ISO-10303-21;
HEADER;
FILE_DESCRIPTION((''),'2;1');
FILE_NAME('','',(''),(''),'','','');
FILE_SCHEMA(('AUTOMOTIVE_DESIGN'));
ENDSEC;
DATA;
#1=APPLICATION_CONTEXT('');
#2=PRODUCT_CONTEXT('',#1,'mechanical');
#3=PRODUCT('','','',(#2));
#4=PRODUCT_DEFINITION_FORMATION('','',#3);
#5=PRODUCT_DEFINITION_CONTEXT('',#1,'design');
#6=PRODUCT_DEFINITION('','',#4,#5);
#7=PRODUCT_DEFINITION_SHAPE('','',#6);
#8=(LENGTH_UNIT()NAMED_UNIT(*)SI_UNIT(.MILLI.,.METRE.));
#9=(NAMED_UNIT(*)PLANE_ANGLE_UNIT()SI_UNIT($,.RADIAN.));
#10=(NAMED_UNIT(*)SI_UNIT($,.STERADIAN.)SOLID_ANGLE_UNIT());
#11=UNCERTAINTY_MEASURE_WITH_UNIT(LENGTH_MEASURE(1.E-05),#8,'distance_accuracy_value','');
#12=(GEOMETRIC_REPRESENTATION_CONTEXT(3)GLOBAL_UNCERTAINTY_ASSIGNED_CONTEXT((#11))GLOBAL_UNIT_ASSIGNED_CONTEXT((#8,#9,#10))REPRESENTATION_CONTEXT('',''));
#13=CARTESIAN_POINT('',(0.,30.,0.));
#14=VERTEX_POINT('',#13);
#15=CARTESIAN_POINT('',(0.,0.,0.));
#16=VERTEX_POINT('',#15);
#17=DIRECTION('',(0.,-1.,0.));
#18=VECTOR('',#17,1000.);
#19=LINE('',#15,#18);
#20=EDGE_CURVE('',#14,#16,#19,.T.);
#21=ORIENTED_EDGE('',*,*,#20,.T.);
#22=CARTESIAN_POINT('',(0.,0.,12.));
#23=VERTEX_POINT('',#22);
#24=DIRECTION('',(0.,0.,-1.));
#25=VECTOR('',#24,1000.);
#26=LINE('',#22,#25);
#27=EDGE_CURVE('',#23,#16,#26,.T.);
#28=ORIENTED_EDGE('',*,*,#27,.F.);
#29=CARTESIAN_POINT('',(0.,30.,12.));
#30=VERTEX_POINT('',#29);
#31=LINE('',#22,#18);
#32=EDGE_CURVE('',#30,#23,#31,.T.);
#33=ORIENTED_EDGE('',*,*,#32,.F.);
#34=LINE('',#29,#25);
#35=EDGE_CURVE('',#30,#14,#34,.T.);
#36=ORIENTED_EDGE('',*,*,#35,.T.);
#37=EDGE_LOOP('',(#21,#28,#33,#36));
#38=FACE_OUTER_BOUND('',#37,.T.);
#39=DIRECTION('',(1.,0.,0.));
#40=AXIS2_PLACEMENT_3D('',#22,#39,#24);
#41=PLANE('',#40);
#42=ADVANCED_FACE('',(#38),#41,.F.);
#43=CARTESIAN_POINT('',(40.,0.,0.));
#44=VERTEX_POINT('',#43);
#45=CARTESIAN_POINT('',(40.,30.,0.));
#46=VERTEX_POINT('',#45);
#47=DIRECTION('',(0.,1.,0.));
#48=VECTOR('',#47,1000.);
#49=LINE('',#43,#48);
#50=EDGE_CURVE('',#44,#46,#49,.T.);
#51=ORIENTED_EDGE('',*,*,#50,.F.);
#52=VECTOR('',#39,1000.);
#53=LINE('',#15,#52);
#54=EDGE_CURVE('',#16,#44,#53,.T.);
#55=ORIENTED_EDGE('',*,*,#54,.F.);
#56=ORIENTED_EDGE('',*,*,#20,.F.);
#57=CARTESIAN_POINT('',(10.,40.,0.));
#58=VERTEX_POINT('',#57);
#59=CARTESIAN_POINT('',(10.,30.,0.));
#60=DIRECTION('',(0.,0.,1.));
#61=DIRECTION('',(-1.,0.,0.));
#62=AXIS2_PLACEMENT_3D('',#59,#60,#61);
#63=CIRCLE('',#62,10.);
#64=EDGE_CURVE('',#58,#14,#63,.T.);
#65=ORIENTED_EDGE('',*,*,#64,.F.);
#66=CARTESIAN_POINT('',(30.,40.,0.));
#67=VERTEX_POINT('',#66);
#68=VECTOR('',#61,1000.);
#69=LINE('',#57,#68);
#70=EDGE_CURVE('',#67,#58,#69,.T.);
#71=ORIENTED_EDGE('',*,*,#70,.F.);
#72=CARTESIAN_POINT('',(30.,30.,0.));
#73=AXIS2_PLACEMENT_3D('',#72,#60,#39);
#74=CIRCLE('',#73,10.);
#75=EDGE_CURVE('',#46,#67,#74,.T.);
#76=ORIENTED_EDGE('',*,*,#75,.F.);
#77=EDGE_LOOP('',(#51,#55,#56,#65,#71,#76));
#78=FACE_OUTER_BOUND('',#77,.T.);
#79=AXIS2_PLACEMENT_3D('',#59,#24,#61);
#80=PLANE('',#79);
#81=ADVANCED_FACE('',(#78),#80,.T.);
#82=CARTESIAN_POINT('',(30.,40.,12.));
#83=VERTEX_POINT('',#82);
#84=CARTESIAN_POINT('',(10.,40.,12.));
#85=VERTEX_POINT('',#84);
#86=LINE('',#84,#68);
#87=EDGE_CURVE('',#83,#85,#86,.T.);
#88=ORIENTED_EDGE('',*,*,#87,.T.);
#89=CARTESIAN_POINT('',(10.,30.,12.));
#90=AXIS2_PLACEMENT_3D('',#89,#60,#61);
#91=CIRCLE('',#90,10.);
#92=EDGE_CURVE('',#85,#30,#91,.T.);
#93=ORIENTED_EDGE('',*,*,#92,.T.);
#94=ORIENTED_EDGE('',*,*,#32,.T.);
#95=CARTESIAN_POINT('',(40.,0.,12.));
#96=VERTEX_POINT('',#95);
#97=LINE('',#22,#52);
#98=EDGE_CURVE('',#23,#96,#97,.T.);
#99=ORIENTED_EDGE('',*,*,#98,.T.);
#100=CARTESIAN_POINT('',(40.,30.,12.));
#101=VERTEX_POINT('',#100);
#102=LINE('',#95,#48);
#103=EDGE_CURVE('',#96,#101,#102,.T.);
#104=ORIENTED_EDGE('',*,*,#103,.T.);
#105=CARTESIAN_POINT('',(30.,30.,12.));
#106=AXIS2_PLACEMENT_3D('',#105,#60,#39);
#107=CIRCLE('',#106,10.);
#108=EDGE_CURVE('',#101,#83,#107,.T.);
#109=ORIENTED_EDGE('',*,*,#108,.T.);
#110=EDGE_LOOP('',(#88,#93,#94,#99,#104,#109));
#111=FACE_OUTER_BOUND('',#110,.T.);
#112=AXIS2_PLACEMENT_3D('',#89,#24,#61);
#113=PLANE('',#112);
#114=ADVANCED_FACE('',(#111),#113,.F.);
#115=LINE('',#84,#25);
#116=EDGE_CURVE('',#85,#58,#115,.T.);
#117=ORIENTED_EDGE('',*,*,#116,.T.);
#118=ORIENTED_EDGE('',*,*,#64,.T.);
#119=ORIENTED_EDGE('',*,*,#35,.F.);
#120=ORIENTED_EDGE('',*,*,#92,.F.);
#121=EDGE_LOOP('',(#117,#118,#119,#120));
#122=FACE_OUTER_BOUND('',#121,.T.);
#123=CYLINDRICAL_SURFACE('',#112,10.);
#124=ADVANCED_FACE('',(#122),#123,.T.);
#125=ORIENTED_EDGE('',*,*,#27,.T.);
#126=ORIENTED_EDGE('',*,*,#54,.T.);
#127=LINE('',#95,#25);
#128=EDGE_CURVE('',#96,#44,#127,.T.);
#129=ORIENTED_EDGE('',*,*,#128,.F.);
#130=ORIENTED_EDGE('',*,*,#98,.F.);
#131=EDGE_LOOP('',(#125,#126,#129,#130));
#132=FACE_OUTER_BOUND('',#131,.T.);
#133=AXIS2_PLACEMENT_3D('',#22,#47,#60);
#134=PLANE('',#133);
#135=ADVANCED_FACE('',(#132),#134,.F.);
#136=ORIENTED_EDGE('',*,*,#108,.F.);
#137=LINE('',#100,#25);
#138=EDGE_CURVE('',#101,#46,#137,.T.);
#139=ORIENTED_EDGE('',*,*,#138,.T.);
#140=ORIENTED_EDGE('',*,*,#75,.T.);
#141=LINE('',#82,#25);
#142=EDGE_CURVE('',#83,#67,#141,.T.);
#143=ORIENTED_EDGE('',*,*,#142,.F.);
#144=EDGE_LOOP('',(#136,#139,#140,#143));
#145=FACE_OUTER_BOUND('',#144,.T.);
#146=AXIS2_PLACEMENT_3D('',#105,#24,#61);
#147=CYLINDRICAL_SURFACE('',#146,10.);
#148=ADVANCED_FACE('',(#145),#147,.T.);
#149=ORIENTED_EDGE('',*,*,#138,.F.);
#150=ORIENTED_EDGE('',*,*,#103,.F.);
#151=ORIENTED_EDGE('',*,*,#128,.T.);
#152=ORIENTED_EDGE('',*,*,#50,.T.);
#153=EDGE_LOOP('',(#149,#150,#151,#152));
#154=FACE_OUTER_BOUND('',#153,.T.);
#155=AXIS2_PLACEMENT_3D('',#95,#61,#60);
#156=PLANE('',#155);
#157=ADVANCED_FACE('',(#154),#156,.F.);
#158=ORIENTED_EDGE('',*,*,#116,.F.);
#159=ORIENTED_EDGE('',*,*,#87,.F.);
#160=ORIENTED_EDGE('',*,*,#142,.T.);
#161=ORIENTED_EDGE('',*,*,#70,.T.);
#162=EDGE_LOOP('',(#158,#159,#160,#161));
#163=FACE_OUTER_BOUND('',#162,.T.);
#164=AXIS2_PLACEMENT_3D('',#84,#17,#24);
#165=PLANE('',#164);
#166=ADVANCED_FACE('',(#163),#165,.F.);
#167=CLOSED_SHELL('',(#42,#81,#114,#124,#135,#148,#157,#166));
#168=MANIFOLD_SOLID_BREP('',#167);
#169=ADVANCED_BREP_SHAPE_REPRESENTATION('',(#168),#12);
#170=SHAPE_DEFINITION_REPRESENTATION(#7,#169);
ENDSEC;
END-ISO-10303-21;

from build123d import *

# Parameters (mm, degrees)
BOSS_EXTRUDE1_DEPTH = 12


with BuildPart() as part:
    # Sketch1 → Boss-Extrude1 (new body)
    with BuildSketch(Plane.XY):
        with BuildLine():
            Line((0, 0), (40, 0))
            Line((40, 0), (40, 30))
            ThreePointArc((40, 30), (37.071067812, 37.071067812), (30, 40))
            Line((30, 40), (10, 40))
            ThreePointArc((10, 40), (2.928932188, 37.071067812), (0, 30))
            Line((0, 30), (0, 0))
        make_face()
    extrude(amount=BOSS_EXTRUDE1_DEPTH)


solid = part.part
